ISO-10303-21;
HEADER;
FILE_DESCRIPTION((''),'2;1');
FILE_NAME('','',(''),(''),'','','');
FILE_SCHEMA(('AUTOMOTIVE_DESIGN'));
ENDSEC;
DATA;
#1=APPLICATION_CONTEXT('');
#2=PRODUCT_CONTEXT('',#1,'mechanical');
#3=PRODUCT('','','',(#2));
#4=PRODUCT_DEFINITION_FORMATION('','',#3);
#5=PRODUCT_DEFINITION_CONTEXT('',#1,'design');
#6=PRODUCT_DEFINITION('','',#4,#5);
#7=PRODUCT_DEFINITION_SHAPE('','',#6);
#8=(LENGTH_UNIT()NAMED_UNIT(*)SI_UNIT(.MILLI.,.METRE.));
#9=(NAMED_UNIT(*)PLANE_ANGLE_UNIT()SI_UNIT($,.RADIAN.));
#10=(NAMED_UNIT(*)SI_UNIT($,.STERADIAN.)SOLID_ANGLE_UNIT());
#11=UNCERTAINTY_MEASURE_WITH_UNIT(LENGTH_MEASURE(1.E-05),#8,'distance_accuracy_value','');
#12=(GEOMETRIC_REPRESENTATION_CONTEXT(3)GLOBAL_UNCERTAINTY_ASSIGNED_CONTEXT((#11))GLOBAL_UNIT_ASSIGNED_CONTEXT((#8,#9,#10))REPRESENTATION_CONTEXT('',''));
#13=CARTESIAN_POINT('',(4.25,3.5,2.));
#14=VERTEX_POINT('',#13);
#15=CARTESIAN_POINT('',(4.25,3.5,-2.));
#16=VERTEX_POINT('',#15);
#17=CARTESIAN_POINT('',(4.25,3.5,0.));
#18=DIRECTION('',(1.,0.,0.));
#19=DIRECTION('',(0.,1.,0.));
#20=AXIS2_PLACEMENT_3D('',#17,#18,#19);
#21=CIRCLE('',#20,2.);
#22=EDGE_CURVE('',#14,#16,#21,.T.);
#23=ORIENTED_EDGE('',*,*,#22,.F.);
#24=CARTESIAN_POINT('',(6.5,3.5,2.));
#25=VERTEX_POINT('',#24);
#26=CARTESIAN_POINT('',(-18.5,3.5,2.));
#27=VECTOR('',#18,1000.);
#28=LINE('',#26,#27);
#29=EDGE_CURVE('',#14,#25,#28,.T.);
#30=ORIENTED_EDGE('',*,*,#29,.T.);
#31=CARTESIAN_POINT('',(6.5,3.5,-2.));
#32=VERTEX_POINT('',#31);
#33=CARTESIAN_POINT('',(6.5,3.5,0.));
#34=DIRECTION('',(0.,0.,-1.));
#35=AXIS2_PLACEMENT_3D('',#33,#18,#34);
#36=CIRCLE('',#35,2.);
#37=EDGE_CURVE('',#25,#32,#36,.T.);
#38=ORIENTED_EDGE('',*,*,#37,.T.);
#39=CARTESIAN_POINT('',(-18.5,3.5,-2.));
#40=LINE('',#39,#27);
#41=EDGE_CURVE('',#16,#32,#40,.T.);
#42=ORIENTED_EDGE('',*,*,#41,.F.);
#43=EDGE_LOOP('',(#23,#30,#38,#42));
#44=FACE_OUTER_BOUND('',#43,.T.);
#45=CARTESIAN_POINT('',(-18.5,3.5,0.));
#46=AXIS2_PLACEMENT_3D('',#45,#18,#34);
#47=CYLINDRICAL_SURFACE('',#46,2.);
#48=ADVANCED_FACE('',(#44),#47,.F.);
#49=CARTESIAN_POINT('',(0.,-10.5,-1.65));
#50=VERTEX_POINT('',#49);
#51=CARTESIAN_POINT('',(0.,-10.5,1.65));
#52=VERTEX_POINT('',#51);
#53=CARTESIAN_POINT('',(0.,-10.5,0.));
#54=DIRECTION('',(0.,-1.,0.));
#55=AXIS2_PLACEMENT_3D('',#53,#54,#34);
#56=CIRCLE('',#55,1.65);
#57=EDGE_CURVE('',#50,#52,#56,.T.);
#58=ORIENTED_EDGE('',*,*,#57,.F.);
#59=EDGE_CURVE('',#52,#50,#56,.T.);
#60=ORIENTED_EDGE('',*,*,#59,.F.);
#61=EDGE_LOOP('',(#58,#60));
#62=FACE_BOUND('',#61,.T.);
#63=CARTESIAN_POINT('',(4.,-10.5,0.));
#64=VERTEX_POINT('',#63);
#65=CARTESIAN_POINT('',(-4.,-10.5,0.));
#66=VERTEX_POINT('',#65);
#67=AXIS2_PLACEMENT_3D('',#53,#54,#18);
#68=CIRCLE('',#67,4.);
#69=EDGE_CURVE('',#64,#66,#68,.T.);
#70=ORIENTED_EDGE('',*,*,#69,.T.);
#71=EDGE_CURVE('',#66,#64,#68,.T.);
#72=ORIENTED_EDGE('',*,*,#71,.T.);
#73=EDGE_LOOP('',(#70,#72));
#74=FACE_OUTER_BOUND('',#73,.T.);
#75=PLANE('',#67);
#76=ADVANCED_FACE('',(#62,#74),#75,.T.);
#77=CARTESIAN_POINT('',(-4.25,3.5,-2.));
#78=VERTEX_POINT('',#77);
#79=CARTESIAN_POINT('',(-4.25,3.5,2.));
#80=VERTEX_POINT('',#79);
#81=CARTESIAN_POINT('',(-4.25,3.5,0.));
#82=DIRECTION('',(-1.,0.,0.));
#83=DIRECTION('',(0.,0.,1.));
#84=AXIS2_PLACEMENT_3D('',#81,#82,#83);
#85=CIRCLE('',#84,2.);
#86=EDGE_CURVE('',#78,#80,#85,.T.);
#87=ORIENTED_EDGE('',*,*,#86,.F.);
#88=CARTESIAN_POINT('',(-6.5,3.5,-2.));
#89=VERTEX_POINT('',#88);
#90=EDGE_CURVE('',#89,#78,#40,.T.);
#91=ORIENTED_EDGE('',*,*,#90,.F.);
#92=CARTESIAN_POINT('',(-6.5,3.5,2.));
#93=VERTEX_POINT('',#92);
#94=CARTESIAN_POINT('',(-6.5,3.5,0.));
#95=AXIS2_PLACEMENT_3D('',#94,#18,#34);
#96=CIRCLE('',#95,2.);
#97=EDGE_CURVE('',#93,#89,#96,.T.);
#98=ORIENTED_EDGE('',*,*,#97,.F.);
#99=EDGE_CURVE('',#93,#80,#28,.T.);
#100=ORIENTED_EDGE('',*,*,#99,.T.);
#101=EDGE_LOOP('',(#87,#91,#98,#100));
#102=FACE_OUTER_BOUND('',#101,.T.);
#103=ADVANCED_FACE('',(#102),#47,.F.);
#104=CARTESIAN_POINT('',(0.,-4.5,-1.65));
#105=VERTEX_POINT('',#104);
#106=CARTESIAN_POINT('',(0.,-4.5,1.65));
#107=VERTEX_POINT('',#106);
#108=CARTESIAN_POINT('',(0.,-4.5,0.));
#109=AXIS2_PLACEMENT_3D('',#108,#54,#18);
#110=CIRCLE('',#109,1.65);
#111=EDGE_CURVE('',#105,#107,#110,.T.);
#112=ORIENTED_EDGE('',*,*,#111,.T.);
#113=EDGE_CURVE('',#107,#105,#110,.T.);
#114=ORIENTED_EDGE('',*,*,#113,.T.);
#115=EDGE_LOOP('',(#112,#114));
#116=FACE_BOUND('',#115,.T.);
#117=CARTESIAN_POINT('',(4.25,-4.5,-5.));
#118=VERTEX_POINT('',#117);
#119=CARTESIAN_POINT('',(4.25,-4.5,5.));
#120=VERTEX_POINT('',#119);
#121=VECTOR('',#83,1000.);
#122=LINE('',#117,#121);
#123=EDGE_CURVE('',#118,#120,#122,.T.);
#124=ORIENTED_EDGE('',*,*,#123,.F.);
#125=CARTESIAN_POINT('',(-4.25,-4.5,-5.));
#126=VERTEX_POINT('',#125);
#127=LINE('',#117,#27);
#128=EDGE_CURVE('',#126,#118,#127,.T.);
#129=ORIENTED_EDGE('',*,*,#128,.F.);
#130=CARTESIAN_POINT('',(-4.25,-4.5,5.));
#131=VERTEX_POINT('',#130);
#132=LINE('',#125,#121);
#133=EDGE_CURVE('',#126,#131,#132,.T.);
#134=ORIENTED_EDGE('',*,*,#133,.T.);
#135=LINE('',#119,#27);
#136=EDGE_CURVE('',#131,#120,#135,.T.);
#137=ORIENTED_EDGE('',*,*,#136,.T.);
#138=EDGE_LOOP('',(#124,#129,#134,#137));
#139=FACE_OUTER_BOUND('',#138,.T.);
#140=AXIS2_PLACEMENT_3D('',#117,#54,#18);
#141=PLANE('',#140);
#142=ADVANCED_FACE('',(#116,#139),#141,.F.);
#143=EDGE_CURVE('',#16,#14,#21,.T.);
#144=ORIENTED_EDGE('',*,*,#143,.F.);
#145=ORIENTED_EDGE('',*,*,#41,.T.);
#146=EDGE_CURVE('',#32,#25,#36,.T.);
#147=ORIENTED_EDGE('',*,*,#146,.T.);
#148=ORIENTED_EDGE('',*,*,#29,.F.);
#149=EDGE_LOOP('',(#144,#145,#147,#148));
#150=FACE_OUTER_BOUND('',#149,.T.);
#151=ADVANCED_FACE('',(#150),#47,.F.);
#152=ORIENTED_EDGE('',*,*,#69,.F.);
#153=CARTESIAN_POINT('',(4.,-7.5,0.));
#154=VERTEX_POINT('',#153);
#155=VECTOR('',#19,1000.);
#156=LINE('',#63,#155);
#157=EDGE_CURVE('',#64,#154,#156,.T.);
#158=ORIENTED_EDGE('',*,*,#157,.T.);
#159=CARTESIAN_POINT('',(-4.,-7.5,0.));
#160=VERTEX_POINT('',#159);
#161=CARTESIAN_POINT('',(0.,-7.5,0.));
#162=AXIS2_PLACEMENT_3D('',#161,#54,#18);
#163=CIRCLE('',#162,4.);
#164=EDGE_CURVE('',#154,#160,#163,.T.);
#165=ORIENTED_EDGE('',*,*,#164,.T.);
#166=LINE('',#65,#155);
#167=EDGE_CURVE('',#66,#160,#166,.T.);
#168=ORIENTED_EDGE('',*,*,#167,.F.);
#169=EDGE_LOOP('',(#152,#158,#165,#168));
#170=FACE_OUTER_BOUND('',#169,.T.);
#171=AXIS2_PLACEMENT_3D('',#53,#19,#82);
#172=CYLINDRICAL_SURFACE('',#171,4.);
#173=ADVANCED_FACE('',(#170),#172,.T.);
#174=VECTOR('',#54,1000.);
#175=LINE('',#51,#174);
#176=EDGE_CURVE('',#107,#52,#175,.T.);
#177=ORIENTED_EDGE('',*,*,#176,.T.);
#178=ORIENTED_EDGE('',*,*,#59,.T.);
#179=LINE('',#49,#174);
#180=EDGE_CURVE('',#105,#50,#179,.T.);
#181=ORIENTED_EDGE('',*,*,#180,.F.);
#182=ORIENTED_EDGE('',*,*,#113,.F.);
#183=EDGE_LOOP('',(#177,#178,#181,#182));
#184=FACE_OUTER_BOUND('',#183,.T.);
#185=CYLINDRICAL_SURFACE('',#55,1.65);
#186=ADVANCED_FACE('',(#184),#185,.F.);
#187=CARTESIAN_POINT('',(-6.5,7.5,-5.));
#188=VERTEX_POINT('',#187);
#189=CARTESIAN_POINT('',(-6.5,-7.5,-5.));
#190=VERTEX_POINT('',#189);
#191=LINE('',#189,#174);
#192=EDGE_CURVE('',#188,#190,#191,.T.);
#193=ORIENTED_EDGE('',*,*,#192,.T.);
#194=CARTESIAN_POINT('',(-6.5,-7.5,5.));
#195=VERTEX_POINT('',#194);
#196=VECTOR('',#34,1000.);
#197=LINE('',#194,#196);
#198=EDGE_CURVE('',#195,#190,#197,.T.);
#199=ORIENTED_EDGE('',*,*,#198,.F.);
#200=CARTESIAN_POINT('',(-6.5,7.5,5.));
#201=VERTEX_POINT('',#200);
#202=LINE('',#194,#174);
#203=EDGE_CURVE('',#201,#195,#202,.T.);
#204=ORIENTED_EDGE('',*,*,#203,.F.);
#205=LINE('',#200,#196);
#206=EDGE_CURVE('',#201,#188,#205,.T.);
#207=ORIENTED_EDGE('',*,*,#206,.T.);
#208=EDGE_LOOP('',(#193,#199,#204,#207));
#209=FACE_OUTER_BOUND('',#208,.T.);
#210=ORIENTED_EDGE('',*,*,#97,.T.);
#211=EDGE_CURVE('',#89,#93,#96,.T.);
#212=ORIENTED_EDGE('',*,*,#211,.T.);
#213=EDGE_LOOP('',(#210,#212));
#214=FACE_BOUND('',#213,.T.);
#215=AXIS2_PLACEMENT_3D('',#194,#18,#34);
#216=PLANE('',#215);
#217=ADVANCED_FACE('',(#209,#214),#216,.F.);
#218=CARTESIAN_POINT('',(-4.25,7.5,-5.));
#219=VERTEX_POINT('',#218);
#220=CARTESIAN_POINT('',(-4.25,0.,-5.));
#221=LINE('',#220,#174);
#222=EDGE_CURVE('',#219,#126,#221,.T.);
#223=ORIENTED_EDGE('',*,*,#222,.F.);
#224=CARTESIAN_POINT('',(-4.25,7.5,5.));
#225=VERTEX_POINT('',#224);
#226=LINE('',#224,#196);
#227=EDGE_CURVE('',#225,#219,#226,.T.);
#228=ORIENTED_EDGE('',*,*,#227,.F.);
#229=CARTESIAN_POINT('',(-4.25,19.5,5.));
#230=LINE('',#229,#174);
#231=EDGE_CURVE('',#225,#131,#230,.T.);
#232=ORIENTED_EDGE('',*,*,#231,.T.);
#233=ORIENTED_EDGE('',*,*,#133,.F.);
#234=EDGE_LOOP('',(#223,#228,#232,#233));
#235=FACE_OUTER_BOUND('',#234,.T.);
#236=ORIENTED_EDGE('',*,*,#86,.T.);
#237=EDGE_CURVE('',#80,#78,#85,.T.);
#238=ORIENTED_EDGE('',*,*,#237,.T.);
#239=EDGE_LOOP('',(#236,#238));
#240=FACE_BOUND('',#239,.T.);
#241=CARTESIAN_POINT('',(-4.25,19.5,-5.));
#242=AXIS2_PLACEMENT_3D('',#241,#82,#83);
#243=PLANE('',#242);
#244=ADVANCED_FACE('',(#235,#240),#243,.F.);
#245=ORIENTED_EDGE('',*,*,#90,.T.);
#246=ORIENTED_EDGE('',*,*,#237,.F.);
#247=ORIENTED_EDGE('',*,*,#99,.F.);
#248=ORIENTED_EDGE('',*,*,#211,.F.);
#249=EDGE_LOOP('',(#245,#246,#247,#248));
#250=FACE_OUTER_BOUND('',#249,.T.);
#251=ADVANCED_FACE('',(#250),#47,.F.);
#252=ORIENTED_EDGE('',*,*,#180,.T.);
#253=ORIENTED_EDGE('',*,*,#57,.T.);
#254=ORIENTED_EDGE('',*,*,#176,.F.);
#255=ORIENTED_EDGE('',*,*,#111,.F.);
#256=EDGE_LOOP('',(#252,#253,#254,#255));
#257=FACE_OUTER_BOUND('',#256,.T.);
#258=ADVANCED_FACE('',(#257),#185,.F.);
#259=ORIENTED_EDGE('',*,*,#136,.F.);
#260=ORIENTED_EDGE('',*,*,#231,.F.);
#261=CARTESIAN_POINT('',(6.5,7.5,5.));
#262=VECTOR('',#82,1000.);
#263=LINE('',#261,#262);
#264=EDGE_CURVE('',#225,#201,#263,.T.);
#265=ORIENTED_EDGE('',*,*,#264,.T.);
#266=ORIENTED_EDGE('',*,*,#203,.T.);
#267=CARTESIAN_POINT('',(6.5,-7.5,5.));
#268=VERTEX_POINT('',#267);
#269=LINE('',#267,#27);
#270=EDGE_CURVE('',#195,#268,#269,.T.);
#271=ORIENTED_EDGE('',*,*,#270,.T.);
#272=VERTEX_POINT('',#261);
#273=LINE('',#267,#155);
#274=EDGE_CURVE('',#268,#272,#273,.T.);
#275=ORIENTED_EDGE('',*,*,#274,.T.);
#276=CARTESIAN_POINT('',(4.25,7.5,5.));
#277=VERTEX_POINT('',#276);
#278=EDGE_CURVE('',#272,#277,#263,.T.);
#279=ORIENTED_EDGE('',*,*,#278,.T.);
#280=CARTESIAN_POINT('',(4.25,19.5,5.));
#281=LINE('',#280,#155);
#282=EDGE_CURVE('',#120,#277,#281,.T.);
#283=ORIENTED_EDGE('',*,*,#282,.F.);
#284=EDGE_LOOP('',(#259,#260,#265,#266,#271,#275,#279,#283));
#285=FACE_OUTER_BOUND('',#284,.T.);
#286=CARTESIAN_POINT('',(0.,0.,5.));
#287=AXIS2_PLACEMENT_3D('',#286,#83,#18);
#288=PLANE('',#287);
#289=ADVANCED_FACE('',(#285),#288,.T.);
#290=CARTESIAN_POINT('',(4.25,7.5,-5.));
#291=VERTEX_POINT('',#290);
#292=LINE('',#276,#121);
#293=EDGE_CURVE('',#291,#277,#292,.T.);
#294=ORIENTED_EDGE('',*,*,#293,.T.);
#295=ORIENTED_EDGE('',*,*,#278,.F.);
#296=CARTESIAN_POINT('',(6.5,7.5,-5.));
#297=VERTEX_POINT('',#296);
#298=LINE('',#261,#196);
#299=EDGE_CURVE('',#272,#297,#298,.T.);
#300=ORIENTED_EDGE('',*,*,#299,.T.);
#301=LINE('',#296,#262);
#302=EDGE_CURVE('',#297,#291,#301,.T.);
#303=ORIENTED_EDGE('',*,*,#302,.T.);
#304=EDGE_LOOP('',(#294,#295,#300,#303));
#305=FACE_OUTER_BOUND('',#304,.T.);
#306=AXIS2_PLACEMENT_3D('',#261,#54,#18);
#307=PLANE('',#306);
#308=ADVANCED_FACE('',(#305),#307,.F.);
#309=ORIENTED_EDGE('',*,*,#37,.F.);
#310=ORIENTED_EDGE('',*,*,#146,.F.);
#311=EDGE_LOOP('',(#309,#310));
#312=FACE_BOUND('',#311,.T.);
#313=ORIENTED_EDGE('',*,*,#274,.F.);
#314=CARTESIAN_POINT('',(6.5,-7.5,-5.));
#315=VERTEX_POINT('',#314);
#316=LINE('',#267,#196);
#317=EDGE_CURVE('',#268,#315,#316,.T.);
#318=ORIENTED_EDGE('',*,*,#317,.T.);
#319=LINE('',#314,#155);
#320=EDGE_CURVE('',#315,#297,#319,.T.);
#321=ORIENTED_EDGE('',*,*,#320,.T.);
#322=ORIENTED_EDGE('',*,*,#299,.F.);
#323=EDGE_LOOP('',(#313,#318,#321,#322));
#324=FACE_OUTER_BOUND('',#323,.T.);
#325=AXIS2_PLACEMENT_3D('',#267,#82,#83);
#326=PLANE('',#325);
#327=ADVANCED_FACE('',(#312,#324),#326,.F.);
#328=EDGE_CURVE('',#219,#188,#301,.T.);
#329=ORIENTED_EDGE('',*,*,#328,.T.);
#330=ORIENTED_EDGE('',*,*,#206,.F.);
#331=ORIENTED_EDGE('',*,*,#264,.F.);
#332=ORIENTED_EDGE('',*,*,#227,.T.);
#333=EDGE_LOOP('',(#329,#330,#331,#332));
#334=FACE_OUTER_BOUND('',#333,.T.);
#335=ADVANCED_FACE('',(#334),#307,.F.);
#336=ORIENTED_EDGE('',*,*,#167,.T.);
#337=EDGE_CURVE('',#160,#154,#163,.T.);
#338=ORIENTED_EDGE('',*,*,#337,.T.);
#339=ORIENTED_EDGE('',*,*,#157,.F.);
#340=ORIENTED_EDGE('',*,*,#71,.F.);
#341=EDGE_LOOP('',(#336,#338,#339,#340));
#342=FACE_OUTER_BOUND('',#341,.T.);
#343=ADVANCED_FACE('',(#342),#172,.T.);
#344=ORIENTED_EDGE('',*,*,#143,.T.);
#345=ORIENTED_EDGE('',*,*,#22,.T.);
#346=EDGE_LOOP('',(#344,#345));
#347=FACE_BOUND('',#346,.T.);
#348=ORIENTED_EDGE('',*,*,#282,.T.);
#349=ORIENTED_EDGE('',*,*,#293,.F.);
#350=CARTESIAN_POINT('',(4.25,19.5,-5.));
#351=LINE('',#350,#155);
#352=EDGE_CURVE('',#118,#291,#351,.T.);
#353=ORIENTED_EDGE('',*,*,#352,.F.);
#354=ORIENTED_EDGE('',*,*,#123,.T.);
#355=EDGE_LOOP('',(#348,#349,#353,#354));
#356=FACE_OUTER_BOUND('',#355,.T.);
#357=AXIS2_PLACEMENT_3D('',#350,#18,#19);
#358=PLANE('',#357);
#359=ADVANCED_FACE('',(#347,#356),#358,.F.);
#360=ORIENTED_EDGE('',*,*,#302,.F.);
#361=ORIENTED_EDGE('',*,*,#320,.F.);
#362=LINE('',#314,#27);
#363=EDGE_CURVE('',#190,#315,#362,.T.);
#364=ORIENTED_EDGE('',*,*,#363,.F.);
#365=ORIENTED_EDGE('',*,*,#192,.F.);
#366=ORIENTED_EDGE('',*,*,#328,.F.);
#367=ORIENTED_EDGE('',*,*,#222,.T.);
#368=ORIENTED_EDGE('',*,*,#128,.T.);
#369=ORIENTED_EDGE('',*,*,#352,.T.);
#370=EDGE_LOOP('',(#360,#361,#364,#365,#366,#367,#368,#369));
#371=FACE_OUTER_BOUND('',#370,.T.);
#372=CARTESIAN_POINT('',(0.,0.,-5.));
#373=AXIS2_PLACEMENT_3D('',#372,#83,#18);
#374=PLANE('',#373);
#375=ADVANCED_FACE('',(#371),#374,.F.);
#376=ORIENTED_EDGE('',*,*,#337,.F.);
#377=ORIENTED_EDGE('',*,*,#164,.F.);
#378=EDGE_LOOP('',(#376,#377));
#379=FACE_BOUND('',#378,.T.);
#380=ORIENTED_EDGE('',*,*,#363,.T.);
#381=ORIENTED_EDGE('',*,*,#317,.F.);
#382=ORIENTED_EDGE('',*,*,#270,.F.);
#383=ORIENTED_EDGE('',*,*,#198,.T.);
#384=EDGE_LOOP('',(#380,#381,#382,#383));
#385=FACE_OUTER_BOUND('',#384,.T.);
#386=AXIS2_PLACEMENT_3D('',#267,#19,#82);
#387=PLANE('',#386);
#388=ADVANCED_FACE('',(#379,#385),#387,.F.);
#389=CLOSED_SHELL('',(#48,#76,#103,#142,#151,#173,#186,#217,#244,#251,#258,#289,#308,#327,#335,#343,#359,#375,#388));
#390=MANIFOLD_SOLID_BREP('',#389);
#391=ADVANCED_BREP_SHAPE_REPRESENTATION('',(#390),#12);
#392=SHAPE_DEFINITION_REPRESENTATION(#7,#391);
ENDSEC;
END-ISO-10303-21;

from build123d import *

# Parameters (mm, degrees)
SKETCH_1_W          = 13
SKETCH_1_H          = 15
EXTRUDE_1_DEPTH     = 5
SKETCH_2_W          = 8.5
SKETCH_2_H          = 24
CUT_EXTRUDE_1_DEPTH = 10
SKETCH_3_R          = 2
CUT_EXTRUDE_2_DEPTH = 25
SKETCH_13_R         = 4
EXTRUDE_2_DEPTH     = 3
M4X0_7_1_D          = 3.3
M4X0_7_1_DEPTH      = 10.1
M4X0_7_1_TIP        = 0.991420021


with BuildPart() as part:
    # 草图1 → 凸台-拉伸1 (new, symmetric)
    with BuildSketch(Plane.XY):
        Rectangle(SKETCH_1_W, SKETCH_1_H)
    extrude(amount=EXTRUDE_1_DEPTH, both=True)

    # 草图2 → 切除-拉伸1 (cut)
    with BuildSketch(Plane.XY.offset(5)):
        with Locations((0, 7.5)):
            Rectangle(SKETCH_2_W, SKETCH_2_H)
    extrude(amount=-CUT_EXTRUDE_1_DEPTH, mode=Mode.SUBTRACT)

    # 草图3 → 切除-拉伸2 (cut)
    with BuildSketch(Plane(origin=(6.5, 0, 0), x_dir=(0, 0, -1), z_dir=(1, 0, 0))):
        with Locations((0, 3.5)):
            Circle(SKETCH_3_R)
    extrude(amount=-CUT_EXTRUDE_2_DEPTH, mode=Mode.SUBTRACT)

    # 草图13 → 凸台-拉伸2 (add)
    with BuildSketch(Plane.XZ.offset(7.5)):
        Circle(SKETCH_13_R)
    extrude(amount=EXTRUDE_2_DEPTH)

    # M4x0.7 螺纹孔1
    with Locations(Plane(origin=(0, -10.5, 0), x_dir=(-1, 0, 0), z_dir=(0, -1, 0))):
        with Locations((0, 0)):
            Hole(M4X0_7_1_D / 2, depth=M4X0_7_1_DEPTH)
            with Locations((0, 0, -(M4X0_7_1_DEPTH + M4X0_7_1_TIP / 2))):  # 118° drill point
                Cone(0, M4X0_7_1_D / 2, M4X0_7_1_TIP, mode=Mode.SUBTRACT)


solid = part.part
